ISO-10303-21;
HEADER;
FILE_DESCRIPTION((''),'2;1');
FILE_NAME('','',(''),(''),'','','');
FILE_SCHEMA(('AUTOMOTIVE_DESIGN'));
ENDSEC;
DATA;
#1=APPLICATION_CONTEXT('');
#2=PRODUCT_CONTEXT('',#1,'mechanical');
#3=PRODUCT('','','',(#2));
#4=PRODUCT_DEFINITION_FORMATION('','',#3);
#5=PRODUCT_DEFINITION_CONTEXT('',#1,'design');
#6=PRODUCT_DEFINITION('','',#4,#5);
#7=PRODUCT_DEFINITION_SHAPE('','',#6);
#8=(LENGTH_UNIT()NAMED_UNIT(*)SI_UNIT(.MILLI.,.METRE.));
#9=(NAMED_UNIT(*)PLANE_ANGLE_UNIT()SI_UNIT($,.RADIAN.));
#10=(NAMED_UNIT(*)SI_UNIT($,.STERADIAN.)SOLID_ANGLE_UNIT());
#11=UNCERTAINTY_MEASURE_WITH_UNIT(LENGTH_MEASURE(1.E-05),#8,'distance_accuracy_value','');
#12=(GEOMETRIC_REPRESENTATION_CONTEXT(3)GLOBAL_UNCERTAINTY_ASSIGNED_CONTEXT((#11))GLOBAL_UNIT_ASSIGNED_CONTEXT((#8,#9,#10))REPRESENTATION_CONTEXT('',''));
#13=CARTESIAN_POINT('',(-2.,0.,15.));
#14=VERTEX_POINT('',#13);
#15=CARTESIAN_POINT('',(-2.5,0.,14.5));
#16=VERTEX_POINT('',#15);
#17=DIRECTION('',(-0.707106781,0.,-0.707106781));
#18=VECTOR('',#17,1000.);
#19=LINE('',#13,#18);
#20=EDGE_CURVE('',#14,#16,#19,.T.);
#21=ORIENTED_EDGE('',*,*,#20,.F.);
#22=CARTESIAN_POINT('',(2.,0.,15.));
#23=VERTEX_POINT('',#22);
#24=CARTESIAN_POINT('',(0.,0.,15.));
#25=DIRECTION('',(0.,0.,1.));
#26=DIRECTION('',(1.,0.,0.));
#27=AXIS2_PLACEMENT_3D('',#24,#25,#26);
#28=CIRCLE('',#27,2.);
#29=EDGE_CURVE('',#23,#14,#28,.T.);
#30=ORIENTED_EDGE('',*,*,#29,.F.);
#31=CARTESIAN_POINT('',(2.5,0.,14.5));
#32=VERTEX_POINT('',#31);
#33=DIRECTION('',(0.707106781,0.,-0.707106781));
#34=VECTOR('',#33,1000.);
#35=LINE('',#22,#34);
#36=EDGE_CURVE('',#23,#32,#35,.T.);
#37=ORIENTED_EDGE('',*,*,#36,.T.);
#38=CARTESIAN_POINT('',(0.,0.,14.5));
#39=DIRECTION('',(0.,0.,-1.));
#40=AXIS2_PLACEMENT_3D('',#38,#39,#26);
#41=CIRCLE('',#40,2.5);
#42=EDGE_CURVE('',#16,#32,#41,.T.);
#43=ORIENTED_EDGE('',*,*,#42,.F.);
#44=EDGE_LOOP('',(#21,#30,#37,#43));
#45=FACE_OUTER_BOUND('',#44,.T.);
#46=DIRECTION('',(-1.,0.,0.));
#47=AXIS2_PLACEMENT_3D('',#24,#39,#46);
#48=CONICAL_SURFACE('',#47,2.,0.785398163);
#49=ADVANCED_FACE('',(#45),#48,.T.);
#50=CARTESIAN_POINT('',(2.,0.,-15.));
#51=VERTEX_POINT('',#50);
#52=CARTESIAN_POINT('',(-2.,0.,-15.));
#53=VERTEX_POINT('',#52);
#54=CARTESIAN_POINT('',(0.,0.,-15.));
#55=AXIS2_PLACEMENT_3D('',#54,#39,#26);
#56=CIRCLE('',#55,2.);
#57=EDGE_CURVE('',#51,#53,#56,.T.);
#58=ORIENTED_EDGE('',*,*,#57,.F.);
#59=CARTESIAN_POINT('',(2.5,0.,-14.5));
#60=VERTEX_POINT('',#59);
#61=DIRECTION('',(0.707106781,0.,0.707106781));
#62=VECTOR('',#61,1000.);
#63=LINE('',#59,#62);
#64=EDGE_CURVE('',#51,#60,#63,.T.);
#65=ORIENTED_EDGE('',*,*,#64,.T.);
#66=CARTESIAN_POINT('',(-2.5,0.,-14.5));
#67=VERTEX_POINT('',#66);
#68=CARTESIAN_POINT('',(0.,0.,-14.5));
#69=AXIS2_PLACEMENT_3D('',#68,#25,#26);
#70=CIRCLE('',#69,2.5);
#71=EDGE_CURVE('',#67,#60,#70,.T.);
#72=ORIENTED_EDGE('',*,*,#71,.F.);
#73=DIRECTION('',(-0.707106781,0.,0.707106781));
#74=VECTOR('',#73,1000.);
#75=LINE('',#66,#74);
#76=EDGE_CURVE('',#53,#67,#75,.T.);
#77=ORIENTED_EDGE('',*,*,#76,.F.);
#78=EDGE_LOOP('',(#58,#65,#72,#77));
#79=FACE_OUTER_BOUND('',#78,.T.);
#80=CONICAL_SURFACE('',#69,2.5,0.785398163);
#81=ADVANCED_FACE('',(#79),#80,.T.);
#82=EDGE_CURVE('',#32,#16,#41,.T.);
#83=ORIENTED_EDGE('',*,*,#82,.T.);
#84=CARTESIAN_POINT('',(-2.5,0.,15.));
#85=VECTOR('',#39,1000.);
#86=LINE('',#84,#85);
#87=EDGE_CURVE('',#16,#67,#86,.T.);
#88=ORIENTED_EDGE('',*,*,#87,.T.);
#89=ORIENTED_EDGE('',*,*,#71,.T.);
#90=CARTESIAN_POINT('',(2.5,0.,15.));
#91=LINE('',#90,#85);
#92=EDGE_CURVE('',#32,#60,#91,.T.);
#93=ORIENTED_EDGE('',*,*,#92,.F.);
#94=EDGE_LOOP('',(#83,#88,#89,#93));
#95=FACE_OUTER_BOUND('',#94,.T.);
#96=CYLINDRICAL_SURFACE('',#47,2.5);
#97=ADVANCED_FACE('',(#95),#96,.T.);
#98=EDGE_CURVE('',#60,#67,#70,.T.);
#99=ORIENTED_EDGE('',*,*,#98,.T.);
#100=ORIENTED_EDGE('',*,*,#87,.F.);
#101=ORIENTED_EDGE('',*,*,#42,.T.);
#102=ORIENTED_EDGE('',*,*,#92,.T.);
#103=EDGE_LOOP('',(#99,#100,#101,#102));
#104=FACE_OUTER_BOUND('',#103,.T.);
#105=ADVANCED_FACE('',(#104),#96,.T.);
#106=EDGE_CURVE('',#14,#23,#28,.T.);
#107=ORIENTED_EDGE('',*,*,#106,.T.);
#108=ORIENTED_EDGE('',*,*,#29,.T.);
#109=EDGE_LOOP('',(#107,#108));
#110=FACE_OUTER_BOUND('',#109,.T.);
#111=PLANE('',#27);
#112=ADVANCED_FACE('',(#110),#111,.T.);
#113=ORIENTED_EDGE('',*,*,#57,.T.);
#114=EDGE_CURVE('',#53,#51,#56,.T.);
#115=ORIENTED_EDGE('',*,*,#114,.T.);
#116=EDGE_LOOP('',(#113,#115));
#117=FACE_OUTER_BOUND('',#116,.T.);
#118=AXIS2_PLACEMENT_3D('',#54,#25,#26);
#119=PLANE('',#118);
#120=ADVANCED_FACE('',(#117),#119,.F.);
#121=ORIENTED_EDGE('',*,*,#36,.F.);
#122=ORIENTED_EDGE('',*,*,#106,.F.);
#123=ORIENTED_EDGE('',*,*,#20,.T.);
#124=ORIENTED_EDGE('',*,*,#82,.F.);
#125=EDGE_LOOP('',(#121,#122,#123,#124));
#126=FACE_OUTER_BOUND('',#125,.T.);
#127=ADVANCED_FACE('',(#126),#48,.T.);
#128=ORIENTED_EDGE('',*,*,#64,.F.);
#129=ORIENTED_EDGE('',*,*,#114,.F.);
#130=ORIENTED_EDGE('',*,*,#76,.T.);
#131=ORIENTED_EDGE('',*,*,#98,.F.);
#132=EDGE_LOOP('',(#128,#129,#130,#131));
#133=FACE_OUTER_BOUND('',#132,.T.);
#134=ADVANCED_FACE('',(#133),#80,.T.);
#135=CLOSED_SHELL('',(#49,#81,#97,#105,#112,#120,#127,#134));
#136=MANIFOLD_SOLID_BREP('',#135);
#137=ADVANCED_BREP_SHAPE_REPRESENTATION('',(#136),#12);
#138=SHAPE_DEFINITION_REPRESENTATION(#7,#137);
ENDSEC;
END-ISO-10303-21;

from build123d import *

# Parameters (mm, degrees)
SKETCH1_R           = 2.5
BOSS_EXTRUDE1_DEPTH = 15
CHAMFER1_SIZE       = 0.5


with BuildPart() as part:
    # Sketch1 → Boss-Extrude1 (new, symmetric)
    with BuildSketch(Plane.XY):
        Circle(SKETCH1_R)
    extrude(amount=BOSS_EXTRUDE1_DEPTH, both=True)

    # Chamfer1
    chamfer1_edges = [part.edges().sort_by_distance(p)[0] for p in [
        (-2.5, 0, -15),
        (-2.5, 0, 15),
    ]]
    chamfer(chamfer1_edges, length=CHAMFER1_SIZE)


solid = part.part
